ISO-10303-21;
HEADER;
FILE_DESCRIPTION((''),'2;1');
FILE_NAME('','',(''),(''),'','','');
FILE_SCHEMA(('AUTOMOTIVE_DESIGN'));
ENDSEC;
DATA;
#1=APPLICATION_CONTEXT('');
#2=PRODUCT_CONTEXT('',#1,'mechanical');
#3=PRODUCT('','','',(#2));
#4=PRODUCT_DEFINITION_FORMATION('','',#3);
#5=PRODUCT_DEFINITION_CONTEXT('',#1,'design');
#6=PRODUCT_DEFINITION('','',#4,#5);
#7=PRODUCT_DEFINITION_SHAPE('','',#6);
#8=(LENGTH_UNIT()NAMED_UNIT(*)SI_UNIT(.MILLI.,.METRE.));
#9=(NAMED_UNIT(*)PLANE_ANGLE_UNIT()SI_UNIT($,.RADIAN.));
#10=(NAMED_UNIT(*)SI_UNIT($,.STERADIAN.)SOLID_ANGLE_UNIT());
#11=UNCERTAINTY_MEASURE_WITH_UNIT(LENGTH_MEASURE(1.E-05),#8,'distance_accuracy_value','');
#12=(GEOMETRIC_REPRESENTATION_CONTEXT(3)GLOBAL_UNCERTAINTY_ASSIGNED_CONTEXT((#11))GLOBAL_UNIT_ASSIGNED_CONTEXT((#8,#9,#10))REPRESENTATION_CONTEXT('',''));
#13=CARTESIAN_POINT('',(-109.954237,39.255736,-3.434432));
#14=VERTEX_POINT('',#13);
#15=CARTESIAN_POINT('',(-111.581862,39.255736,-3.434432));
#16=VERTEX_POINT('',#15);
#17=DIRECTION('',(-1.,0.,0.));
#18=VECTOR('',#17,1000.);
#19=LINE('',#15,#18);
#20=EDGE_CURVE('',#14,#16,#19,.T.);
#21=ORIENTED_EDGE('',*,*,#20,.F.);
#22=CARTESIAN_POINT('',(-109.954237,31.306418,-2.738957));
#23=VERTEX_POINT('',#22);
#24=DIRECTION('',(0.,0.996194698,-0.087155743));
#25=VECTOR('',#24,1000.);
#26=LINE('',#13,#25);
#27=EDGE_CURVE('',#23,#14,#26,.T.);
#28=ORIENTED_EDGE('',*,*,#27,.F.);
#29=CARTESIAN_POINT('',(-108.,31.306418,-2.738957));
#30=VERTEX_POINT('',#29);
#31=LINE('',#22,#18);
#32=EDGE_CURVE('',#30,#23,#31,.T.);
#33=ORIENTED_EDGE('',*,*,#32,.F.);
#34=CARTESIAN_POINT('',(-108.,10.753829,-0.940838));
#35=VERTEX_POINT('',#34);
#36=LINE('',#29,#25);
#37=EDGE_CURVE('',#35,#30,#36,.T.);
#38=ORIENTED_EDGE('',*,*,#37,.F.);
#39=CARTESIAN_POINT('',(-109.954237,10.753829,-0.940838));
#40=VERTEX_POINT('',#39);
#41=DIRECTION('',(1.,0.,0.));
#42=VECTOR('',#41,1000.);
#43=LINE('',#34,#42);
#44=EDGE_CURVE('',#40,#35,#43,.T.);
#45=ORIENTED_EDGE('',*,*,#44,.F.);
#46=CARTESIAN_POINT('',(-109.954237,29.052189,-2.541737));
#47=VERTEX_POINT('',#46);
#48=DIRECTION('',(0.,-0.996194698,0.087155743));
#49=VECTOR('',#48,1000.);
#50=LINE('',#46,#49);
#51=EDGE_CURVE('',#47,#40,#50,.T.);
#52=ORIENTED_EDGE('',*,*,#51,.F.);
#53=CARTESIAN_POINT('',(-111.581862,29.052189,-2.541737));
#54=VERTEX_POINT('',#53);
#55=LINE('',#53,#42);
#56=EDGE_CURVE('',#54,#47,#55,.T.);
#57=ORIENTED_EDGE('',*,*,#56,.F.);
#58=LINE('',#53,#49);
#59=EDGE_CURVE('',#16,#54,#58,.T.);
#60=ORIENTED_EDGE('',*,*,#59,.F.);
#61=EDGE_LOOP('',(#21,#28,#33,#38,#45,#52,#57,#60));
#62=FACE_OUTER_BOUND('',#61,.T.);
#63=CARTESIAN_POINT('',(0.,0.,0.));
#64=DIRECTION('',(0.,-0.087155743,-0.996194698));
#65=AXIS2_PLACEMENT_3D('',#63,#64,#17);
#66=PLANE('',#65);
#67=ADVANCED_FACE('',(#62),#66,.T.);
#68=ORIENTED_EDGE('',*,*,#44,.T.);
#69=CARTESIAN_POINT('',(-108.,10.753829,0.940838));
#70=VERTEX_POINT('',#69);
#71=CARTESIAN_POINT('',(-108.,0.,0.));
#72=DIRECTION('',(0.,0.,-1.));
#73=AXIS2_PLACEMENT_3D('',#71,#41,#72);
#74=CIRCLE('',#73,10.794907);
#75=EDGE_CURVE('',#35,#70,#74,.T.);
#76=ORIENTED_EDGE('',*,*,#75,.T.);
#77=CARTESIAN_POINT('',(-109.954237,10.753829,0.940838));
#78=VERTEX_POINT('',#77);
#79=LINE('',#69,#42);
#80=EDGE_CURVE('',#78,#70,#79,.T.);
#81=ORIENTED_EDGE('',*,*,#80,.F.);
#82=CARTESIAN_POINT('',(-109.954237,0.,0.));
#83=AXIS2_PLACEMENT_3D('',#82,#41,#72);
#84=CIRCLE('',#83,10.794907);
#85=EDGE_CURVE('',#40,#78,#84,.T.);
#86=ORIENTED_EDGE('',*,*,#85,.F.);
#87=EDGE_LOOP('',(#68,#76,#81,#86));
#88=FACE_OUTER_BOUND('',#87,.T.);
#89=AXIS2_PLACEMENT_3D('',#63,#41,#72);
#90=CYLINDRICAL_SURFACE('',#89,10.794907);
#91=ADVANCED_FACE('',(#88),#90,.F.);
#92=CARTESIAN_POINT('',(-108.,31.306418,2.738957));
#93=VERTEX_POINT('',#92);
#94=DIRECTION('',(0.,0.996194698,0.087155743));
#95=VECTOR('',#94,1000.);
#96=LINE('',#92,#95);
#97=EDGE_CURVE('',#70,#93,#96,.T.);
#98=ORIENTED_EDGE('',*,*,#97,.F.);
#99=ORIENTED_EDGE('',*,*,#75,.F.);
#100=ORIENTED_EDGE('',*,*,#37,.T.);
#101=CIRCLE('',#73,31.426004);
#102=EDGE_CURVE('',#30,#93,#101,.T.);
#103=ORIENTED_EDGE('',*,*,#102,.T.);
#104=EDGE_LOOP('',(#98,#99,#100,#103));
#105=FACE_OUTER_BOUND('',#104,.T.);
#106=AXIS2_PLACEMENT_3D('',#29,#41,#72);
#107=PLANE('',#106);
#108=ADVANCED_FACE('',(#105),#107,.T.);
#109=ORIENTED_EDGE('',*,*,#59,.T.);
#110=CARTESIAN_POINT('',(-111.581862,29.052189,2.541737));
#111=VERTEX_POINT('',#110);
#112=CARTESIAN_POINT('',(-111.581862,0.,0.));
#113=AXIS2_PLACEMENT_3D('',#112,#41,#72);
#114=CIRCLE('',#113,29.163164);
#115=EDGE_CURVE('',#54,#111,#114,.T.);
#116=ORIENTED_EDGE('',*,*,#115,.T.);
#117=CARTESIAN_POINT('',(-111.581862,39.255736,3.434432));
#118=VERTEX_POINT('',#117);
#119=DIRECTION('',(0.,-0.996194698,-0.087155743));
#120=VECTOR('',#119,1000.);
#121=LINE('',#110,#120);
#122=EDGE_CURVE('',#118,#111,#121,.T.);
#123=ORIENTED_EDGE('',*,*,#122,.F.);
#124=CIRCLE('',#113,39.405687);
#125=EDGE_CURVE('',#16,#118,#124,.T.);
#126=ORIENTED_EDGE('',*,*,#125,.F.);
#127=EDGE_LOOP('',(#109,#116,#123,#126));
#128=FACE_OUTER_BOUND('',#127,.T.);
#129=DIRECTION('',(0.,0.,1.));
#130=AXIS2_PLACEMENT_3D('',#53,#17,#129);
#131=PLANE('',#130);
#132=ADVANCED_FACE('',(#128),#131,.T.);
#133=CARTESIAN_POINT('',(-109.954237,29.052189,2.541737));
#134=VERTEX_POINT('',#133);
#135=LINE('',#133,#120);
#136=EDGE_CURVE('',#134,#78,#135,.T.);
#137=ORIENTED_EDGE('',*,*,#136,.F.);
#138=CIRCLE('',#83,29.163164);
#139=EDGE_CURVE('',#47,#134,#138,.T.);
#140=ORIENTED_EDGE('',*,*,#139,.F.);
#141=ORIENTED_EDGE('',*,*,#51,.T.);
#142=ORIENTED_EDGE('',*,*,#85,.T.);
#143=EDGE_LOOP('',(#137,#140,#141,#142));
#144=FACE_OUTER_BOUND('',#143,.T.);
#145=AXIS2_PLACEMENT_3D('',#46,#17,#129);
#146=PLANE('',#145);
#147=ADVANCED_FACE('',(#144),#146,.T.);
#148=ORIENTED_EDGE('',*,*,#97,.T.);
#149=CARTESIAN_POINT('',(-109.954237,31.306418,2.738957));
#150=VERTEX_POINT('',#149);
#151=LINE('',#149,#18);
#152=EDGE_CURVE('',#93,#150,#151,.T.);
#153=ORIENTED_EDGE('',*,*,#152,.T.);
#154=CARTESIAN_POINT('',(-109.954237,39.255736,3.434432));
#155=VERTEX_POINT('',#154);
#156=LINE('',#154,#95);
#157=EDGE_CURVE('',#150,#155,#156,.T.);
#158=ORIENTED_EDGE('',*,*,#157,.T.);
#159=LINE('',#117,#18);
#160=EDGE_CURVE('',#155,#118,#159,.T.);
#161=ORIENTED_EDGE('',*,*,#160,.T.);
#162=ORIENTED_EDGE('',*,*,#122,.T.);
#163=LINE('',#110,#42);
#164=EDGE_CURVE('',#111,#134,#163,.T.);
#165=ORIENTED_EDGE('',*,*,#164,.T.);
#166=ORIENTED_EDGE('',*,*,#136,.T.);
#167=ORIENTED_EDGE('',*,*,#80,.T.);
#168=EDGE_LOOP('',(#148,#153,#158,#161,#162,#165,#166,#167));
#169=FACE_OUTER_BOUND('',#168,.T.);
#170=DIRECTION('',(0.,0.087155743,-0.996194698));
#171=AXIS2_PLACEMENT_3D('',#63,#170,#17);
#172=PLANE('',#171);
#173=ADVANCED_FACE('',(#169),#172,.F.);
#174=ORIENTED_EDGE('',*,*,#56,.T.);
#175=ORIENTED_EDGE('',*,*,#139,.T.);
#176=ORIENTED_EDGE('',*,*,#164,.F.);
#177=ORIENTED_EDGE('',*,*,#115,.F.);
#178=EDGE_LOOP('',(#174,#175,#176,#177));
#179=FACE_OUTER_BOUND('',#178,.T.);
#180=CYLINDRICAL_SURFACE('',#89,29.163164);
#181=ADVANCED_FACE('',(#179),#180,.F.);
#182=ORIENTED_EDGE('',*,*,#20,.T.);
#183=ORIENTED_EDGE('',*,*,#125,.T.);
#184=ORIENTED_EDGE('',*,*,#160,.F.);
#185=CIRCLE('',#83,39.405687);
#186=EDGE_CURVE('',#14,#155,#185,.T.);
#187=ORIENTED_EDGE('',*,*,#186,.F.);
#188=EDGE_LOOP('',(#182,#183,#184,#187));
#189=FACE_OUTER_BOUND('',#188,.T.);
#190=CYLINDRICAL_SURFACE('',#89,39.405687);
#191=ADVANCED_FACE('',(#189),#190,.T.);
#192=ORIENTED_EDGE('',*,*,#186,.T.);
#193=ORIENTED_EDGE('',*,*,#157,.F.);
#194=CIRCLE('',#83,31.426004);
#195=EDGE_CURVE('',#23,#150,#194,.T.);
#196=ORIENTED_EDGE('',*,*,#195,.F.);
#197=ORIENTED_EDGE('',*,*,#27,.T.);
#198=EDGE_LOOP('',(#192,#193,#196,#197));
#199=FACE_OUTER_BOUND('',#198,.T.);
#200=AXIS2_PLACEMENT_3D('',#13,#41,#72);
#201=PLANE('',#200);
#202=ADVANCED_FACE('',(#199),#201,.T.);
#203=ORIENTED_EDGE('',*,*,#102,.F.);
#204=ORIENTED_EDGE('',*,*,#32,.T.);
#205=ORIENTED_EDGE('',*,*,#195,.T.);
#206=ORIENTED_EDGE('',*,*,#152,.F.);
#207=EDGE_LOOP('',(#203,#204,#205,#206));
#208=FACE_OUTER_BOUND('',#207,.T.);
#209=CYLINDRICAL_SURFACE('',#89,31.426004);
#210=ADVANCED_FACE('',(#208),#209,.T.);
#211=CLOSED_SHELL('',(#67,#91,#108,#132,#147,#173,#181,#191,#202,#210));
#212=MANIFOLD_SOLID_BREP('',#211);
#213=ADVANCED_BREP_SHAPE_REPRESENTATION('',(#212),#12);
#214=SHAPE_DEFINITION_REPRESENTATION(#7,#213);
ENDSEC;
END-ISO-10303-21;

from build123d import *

# Parameters (mm, degrees)
REVOLVE1_ANGLE = 10


with BuildPart() as part:
    # Sketch1 → Revolve1 (revolve, symmetric)
    with BuildSketch(Plane.XY) as revolve1_sk:
        Polygon((-109.954236571, 39.405686592), (-109.954236571, 31.426003585), (-108, 31.426003585), (-108, 10.794907178), (-109.954236571, 10.794907178), (-109.954236571, 29.163164129), (-111.581862319, 29.163164129), (-111.581862319, 39.405686592), align=None)
    revolve(axis=Axis((0, 0, 0), (-1, 0, 0)), revolution_arc=REVOLVE1_ANGLE / 2)
    revolve(revolve1_sk.sketch, axis=Axis((0, 0, 0), (1, 0, 0)), revolution_arc=REVOLVE1_ANGLE / 2)


solid = part.part
